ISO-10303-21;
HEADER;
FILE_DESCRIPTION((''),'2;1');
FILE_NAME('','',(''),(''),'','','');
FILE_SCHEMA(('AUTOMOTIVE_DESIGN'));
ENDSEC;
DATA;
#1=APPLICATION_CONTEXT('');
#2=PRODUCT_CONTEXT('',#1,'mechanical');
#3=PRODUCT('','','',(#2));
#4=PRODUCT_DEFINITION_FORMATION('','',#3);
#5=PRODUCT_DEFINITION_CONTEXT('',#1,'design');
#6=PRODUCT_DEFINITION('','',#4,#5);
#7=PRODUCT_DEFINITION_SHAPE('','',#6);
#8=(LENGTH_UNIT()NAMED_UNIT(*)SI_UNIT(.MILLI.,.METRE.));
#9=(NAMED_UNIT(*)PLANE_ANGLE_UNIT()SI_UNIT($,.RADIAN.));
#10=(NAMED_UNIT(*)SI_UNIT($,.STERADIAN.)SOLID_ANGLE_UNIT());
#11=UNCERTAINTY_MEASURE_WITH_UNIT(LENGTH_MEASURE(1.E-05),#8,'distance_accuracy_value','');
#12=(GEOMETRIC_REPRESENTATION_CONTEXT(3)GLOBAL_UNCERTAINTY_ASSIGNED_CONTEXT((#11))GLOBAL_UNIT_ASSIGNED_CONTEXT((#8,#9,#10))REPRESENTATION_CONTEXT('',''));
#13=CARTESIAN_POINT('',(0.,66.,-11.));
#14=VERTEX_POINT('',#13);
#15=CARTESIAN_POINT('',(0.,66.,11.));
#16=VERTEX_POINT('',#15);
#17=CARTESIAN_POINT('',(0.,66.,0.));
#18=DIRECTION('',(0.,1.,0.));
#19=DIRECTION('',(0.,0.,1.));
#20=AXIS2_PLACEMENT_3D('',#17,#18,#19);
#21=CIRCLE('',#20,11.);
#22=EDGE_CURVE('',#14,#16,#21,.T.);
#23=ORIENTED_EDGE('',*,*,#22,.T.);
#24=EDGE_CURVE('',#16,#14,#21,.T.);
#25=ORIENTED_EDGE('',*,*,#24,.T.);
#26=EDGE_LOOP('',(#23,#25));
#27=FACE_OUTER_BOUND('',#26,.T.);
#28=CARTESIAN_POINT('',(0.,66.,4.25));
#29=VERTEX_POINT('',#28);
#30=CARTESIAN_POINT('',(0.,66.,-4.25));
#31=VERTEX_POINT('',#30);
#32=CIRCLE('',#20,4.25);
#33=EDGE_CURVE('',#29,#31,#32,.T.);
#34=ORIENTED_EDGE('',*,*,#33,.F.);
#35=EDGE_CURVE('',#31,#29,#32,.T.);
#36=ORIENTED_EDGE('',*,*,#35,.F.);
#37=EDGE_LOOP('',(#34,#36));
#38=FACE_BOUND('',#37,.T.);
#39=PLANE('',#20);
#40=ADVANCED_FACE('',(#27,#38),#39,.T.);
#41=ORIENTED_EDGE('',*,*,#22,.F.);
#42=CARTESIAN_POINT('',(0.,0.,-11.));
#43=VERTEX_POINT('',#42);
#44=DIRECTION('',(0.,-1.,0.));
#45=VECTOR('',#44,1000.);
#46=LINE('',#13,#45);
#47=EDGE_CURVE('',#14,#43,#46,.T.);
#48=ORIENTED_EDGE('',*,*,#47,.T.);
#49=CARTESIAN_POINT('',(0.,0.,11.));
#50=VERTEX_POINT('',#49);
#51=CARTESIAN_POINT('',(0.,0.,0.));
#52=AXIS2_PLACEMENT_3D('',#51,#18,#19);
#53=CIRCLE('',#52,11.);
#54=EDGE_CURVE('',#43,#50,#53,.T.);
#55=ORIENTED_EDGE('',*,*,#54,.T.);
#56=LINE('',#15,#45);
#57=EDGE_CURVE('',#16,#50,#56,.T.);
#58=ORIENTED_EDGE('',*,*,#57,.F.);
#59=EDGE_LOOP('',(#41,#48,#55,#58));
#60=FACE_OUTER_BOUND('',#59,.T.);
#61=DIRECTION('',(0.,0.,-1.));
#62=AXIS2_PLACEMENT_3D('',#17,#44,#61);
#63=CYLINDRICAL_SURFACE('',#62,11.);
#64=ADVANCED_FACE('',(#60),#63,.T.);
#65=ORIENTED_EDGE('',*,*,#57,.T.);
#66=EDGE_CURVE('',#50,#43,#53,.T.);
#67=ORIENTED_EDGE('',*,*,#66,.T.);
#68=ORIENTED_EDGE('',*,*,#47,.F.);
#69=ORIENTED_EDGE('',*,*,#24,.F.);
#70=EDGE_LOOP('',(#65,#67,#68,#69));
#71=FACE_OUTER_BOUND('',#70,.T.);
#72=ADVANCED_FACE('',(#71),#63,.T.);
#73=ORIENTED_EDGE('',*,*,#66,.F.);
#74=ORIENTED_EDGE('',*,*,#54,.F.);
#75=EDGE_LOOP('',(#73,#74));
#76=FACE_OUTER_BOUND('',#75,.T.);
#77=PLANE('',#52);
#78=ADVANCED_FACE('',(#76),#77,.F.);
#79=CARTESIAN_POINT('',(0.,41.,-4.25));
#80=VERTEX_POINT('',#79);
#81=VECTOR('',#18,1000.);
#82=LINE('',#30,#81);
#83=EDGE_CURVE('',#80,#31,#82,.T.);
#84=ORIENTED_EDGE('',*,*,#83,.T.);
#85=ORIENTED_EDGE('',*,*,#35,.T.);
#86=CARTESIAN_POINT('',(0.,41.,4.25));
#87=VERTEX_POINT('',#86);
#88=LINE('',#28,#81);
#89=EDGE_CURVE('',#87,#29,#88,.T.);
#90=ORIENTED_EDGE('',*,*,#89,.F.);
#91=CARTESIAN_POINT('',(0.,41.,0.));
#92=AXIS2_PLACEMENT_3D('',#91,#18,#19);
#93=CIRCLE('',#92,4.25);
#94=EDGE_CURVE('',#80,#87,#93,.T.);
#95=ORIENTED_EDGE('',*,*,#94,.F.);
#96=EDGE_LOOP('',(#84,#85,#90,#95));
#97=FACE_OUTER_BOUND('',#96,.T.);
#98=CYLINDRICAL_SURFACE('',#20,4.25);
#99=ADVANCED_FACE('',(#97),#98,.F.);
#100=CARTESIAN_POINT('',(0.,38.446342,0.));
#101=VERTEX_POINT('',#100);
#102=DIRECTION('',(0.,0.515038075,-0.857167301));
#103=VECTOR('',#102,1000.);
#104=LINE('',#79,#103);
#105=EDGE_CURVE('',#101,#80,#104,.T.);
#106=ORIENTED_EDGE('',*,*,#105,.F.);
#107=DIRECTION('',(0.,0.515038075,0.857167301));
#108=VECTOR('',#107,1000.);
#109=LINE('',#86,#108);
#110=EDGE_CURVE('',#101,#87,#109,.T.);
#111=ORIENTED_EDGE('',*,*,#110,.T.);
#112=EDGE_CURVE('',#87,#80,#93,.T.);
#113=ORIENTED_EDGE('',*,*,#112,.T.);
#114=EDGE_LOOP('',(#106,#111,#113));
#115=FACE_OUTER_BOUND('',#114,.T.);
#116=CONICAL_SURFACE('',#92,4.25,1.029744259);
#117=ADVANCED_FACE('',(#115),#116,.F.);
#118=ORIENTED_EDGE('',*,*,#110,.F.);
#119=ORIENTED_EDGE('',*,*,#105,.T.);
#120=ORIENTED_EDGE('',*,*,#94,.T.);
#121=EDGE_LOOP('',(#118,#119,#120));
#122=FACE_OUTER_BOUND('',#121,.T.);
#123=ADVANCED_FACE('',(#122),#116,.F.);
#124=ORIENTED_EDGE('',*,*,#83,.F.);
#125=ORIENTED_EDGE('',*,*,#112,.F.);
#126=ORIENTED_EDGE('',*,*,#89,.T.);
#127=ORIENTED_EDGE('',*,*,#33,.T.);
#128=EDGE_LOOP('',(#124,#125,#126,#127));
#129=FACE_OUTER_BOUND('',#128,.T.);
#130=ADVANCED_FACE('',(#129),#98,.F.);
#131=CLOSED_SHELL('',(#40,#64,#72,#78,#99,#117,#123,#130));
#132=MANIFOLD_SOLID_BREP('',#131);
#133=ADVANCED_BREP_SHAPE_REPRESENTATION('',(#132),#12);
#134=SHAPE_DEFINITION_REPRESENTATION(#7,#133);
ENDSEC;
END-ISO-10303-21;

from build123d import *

# Parameters (mm, degrees)
SKETCH1_R              = 11
BOSS_EXTRUDE1_DEPTH    = 66
M10_TAPPED_HOLE1_D     = 8.5
M10_TAPPED_HOLE1_DEPTH = 25
M10_TAPPED_HOLE1_TIP   = 2.553657631


with BuildPart() as part:
    # Sketch1 → Boss-Extrude1 (new body)
    with BuildSketch(Plane(origin=(0, 0, 0), x_dir=(1, 0, 0), z_dir=(0, 1, 0))):
        with Locations(Location((0, 0, 0), (0, 0, 270))):
            Circle(SKETCH1_R)
    extrude(amount=BOSS_EXTRUDE1_DEPTH)

    # M10 Tapped Hole1
    with Locations(Plane(origin=(0, 66, 0), x_dir=(1, 0, 0), z_dir=(0, 1, 0))):
        with Locations((0, 0)):
            Hole(M10_TAPPED_HOLE1_D / 2, depth=M10_TAPPED_HOLE1_DEPTH)
            with Locations((0, 0, -(M10_TAPPED_HOLE1_DEPTH + M10_TAPPED_HOLE1_TIP / 2))):  # 118° drill point
                Cone(0, M10_TAPPED_HOLE1_D / 2, M10_TAPPED_HOLE1_TIP, mode=Mode.SUBTRACT)


solid = part.part
